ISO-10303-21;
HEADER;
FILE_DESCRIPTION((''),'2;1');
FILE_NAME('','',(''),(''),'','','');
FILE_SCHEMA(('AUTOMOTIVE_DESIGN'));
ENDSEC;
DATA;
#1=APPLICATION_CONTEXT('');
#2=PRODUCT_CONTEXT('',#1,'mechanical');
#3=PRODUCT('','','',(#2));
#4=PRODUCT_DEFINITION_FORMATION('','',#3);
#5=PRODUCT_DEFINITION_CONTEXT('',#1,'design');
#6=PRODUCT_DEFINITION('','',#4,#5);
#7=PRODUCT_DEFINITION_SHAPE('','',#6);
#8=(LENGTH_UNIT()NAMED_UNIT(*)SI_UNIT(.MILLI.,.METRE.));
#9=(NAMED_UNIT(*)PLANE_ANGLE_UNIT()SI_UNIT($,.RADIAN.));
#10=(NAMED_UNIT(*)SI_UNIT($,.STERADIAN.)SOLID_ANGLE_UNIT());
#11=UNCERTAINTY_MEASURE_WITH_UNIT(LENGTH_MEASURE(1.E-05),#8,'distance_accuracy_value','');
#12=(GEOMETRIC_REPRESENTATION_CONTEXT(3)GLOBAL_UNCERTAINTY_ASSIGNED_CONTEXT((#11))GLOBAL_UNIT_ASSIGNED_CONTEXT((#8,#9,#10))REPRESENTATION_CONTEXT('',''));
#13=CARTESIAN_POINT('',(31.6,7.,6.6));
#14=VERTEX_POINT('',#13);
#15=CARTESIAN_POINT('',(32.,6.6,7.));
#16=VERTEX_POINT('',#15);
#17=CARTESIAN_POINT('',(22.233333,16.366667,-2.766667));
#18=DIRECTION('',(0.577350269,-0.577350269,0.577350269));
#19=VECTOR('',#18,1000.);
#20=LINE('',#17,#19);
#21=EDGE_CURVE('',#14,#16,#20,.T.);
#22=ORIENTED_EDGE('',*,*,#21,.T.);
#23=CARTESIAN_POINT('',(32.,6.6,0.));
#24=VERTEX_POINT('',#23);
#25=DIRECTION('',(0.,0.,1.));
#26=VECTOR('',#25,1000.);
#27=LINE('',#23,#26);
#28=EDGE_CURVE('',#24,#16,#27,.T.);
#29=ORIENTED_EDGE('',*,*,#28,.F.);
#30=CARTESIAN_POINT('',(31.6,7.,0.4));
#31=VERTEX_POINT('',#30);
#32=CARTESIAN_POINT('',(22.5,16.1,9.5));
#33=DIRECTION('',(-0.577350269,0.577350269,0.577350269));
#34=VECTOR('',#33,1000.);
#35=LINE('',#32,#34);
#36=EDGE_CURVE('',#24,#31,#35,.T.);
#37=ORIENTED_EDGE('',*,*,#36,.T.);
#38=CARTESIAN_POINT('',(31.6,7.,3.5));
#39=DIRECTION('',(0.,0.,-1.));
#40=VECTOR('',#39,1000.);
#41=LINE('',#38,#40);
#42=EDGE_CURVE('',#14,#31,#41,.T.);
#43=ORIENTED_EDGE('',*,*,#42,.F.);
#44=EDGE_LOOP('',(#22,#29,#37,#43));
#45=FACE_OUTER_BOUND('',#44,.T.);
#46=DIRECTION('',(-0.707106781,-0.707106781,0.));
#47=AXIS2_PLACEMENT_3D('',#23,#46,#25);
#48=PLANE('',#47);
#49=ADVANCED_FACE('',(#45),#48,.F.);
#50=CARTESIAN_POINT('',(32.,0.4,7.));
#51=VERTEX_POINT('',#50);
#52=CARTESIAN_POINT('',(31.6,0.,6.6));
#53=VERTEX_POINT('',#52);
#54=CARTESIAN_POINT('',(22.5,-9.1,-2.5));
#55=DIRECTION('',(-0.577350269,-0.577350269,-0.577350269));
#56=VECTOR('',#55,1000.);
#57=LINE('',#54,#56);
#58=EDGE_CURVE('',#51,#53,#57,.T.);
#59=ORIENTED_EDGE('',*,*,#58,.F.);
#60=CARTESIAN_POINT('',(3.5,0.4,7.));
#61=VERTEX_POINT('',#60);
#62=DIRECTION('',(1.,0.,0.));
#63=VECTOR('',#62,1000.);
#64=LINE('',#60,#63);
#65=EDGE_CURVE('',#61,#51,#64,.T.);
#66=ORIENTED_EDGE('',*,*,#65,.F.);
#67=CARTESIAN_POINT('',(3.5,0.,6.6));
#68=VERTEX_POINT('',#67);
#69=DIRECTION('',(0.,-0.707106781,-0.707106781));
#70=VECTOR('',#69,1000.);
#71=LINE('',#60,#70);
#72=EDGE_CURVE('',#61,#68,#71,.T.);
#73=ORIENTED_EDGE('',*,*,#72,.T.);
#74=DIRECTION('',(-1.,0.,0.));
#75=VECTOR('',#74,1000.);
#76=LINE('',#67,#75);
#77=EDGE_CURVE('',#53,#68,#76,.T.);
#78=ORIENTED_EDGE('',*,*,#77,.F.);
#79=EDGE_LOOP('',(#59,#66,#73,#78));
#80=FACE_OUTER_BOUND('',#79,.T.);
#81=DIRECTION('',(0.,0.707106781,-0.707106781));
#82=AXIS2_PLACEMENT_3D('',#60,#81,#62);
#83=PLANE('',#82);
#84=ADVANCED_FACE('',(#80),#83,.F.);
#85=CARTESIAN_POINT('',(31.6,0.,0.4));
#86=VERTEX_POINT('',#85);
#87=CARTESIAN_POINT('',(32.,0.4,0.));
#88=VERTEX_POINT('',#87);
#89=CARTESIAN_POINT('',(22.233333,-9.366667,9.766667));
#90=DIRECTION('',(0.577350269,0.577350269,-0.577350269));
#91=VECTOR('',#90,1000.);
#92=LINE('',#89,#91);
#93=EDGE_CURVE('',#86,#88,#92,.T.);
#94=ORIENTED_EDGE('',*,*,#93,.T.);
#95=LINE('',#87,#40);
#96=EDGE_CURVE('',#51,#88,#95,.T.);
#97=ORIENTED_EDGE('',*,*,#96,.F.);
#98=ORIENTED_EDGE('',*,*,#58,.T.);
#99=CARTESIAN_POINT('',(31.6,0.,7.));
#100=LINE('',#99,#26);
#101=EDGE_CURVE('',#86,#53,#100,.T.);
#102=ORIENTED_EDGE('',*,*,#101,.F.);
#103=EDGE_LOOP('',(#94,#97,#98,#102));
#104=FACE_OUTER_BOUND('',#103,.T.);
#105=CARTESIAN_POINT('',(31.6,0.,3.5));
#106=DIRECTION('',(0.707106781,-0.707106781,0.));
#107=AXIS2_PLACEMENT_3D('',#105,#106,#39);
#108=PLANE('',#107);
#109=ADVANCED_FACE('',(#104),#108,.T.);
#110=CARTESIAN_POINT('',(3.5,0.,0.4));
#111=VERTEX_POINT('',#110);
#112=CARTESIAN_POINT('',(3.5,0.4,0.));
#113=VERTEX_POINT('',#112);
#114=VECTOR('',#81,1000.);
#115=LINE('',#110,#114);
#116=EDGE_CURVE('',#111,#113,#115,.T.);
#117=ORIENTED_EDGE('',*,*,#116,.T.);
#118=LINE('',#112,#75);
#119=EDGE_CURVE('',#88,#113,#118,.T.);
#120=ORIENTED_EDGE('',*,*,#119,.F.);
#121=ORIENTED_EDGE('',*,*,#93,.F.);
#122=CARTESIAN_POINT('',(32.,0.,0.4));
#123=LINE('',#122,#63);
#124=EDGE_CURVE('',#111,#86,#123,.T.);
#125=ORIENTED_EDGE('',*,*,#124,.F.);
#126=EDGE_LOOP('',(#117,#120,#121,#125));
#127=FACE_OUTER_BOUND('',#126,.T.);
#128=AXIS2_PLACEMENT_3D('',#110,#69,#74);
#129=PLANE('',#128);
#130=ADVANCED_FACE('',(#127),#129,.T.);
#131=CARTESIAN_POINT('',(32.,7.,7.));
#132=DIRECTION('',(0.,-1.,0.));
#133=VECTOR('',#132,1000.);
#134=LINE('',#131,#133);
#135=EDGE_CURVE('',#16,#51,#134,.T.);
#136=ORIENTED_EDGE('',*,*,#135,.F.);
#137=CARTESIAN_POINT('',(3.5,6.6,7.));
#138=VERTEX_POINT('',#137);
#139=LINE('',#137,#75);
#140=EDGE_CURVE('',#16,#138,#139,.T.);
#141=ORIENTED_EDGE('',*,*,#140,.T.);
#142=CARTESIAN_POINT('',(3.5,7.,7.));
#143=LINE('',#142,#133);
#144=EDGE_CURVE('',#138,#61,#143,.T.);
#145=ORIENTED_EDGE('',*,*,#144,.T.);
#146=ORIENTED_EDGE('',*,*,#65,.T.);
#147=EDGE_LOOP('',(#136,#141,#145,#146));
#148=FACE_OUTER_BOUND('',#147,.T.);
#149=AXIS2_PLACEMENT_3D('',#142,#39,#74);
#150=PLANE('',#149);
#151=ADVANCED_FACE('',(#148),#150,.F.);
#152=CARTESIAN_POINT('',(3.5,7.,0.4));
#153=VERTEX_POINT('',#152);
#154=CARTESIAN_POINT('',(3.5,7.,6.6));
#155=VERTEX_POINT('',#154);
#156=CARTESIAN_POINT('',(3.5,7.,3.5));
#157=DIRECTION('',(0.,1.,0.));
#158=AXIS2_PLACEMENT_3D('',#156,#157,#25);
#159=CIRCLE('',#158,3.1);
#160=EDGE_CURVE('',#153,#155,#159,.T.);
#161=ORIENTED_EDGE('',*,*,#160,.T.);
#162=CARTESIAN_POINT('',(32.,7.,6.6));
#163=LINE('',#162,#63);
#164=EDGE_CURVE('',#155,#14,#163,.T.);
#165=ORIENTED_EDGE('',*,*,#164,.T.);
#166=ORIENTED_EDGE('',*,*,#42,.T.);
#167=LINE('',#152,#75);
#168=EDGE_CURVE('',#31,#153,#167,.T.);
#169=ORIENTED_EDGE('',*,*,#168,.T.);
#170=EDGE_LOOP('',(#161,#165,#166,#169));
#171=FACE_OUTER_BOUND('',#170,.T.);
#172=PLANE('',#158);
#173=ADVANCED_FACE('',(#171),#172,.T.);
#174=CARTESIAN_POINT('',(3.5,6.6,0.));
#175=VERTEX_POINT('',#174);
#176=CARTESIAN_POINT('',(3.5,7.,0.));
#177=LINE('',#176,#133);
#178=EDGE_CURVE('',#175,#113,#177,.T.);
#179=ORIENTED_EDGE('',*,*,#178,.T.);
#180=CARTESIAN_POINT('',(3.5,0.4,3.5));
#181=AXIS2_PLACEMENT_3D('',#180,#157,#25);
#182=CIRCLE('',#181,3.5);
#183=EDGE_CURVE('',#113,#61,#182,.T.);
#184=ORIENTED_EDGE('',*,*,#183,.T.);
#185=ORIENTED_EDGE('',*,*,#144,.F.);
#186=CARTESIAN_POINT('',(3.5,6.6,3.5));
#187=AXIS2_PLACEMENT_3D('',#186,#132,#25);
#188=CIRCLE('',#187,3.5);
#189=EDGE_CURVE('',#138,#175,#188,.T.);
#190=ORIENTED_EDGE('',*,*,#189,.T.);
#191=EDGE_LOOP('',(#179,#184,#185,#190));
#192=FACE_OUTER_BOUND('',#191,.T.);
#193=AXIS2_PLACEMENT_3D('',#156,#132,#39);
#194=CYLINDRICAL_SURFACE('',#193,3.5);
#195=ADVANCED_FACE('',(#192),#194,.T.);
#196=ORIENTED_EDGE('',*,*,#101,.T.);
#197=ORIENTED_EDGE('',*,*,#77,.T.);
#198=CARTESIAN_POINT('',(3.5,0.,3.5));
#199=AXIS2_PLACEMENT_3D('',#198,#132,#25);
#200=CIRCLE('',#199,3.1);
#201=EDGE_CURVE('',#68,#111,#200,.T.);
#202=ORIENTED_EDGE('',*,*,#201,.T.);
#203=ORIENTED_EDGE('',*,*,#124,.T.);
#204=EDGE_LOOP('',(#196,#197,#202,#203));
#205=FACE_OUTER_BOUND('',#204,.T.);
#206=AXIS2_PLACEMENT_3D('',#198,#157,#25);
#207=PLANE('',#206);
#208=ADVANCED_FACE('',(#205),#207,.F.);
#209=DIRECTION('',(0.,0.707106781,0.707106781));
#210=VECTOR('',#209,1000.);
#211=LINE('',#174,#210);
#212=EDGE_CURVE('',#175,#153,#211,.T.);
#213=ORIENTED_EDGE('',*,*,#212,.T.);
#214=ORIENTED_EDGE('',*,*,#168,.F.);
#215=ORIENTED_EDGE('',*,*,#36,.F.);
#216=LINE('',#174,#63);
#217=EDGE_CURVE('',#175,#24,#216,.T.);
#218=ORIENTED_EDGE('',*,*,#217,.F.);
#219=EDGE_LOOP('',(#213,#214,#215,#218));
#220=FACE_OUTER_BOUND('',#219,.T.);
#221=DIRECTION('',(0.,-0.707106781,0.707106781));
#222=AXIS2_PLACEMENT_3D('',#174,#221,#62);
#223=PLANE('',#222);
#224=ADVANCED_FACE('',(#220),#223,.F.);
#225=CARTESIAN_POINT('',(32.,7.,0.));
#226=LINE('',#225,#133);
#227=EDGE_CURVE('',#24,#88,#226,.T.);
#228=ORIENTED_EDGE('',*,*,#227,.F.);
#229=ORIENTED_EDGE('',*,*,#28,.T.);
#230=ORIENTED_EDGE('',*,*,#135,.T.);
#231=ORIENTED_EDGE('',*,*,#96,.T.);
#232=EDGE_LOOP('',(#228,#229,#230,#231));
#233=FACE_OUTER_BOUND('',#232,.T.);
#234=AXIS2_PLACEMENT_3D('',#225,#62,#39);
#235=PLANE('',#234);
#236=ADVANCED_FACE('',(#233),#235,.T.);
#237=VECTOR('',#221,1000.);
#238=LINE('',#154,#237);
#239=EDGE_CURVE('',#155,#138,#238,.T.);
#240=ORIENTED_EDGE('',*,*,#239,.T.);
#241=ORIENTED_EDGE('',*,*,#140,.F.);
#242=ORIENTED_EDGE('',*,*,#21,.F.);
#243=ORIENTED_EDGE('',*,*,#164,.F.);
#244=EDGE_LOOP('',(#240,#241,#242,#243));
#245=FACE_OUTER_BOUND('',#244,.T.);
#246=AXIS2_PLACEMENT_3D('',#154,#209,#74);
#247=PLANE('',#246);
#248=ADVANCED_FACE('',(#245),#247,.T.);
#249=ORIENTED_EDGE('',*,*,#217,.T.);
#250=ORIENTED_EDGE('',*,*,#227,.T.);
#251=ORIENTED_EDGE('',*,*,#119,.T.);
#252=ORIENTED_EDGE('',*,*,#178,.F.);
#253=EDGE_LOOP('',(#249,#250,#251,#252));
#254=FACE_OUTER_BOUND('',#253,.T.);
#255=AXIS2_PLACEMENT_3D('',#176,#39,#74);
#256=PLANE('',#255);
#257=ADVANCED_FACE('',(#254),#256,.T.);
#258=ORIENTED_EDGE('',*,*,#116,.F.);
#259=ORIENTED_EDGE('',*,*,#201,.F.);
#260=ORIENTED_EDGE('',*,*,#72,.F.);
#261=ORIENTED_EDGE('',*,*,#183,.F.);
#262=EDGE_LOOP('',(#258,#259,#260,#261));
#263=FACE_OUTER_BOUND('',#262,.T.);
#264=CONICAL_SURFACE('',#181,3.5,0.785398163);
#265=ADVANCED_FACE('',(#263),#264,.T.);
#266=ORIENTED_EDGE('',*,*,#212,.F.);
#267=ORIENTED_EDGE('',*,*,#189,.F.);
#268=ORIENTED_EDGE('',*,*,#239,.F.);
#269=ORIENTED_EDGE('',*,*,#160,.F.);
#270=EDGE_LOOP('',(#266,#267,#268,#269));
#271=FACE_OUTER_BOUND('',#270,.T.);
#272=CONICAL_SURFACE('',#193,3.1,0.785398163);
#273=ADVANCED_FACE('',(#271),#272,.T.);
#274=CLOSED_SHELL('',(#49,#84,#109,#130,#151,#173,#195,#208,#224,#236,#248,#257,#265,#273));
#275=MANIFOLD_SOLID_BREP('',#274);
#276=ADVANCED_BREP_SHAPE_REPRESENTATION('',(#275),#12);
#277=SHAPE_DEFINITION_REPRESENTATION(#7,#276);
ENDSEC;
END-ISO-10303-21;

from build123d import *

# Parameters (mm, degrees)
EXTRUDE_1_DEPTH = 7
CHAMFER_1_SIZE  = 0.4


with BuildPart() as part:
    # 草图1 → 凸台-拉伸1 (new body)
    with BuildSketch(Plane(origin=(0, 0, 0), x_dir=(1, 0, 0), z_dir=(0, 1, 0))):
        with BuildLine():
            Line((3.5, 0), (32, 0))
            Line((32, 0), (32, -7))
            Line((32, -7), (3.5, -7))
            ThreePointArc((3.5, -7), (0, -3.5), (3.5, 0))
        make_face()
    extrude(amount=EXTRUDE_1_DEPTH)

    # 倒角1
    chamfer_1_edges = [part.edges().sort_by_distance(p)[0] for p in [
        (32, 7, 3.5),
        (17.75, 7, 0),
        (0, 7, 3.5),
        (17.75, 0, 0),
        (32, 0, 3.5),
        (17.75, 0, 7),
        (0, 0, 3.5),
        (17.75, 7, 7),
    ]]
    chamfer(chamfer_1_edges, length=CHAMFER_1_SIZE)


solid = part.part
